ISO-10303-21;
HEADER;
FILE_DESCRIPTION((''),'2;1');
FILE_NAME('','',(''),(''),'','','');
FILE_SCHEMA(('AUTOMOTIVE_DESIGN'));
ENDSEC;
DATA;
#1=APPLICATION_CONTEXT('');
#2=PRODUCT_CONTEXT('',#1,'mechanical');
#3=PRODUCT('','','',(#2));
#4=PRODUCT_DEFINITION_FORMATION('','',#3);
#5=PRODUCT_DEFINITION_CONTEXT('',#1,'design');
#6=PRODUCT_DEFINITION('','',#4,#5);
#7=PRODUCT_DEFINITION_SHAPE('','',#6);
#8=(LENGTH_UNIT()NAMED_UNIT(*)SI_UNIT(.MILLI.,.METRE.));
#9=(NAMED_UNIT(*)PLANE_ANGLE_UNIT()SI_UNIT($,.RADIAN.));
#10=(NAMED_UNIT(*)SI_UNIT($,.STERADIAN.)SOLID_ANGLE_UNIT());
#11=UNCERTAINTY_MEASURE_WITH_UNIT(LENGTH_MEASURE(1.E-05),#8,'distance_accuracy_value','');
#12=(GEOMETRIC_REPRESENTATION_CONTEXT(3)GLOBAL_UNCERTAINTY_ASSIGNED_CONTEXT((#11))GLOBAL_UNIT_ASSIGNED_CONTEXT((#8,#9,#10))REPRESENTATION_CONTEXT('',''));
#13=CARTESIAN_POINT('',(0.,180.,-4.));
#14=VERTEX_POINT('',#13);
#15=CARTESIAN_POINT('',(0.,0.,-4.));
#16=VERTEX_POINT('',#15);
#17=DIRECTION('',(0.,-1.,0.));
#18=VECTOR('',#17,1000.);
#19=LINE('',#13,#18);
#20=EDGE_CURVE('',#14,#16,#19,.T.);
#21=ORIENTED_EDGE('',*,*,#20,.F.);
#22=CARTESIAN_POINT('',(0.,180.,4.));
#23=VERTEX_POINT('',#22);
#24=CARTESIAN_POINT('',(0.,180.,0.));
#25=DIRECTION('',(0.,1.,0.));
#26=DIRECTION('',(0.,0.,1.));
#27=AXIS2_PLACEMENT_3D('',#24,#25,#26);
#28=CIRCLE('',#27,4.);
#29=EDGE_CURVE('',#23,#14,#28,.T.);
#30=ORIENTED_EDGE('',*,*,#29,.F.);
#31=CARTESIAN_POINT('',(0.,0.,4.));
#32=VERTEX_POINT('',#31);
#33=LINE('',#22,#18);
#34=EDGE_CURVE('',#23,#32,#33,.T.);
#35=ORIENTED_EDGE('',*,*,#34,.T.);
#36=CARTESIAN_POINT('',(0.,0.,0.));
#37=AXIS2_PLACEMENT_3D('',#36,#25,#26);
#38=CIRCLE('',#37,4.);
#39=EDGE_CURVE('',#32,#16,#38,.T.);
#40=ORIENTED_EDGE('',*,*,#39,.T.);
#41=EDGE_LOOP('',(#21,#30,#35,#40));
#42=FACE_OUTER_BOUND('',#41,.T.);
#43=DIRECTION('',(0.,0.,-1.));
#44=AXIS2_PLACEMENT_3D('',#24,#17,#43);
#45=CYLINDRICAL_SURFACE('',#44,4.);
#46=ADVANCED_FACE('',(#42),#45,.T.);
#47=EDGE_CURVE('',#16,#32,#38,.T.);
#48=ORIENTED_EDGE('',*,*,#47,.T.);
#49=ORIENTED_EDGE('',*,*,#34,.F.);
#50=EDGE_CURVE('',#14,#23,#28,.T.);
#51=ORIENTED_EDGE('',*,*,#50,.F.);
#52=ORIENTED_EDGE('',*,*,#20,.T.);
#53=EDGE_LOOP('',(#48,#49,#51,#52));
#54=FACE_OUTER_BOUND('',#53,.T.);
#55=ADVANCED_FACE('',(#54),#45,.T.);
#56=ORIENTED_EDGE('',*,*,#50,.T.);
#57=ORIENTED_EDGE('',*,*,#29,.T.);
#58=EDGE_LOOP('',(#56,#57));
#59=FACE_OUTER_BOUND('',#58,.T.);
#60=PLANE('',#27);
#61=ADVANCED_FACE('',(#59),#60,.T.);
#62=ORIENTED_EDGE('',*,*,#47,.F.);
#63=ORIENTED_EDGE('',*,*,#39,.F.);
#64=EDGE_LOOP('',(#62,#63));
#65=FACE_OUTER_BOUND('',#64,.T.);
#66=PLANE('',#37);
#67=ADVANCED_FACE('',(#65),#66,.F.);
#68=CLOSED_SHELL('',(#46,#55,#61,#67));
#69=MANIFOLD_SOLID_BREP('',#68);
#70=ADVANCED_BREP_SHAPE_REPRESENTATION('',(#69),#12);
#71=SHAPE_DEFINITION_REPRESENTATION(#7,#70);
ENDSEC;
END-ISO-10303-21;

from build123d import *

# Parameters (mm, degrees)
SKETCH_1_R      = 4
EXTRUDE_1_DEPTH = 180


with BuildPart() as part:
    # 草图1 → 凸台-拉伸1 (new body)
    with BuildSketch(Plane(origin=(0, 0, 0), x_dir=(1, 0, 0), z_dir=(0, 1, 0))):
        with Locations(Location((0, 0, 0), (0, 0, 90))):
            Circle(SKETCH_1_R)
    extrude(amount=EXTRUDE_1_DEPTH)


solid = part.part
